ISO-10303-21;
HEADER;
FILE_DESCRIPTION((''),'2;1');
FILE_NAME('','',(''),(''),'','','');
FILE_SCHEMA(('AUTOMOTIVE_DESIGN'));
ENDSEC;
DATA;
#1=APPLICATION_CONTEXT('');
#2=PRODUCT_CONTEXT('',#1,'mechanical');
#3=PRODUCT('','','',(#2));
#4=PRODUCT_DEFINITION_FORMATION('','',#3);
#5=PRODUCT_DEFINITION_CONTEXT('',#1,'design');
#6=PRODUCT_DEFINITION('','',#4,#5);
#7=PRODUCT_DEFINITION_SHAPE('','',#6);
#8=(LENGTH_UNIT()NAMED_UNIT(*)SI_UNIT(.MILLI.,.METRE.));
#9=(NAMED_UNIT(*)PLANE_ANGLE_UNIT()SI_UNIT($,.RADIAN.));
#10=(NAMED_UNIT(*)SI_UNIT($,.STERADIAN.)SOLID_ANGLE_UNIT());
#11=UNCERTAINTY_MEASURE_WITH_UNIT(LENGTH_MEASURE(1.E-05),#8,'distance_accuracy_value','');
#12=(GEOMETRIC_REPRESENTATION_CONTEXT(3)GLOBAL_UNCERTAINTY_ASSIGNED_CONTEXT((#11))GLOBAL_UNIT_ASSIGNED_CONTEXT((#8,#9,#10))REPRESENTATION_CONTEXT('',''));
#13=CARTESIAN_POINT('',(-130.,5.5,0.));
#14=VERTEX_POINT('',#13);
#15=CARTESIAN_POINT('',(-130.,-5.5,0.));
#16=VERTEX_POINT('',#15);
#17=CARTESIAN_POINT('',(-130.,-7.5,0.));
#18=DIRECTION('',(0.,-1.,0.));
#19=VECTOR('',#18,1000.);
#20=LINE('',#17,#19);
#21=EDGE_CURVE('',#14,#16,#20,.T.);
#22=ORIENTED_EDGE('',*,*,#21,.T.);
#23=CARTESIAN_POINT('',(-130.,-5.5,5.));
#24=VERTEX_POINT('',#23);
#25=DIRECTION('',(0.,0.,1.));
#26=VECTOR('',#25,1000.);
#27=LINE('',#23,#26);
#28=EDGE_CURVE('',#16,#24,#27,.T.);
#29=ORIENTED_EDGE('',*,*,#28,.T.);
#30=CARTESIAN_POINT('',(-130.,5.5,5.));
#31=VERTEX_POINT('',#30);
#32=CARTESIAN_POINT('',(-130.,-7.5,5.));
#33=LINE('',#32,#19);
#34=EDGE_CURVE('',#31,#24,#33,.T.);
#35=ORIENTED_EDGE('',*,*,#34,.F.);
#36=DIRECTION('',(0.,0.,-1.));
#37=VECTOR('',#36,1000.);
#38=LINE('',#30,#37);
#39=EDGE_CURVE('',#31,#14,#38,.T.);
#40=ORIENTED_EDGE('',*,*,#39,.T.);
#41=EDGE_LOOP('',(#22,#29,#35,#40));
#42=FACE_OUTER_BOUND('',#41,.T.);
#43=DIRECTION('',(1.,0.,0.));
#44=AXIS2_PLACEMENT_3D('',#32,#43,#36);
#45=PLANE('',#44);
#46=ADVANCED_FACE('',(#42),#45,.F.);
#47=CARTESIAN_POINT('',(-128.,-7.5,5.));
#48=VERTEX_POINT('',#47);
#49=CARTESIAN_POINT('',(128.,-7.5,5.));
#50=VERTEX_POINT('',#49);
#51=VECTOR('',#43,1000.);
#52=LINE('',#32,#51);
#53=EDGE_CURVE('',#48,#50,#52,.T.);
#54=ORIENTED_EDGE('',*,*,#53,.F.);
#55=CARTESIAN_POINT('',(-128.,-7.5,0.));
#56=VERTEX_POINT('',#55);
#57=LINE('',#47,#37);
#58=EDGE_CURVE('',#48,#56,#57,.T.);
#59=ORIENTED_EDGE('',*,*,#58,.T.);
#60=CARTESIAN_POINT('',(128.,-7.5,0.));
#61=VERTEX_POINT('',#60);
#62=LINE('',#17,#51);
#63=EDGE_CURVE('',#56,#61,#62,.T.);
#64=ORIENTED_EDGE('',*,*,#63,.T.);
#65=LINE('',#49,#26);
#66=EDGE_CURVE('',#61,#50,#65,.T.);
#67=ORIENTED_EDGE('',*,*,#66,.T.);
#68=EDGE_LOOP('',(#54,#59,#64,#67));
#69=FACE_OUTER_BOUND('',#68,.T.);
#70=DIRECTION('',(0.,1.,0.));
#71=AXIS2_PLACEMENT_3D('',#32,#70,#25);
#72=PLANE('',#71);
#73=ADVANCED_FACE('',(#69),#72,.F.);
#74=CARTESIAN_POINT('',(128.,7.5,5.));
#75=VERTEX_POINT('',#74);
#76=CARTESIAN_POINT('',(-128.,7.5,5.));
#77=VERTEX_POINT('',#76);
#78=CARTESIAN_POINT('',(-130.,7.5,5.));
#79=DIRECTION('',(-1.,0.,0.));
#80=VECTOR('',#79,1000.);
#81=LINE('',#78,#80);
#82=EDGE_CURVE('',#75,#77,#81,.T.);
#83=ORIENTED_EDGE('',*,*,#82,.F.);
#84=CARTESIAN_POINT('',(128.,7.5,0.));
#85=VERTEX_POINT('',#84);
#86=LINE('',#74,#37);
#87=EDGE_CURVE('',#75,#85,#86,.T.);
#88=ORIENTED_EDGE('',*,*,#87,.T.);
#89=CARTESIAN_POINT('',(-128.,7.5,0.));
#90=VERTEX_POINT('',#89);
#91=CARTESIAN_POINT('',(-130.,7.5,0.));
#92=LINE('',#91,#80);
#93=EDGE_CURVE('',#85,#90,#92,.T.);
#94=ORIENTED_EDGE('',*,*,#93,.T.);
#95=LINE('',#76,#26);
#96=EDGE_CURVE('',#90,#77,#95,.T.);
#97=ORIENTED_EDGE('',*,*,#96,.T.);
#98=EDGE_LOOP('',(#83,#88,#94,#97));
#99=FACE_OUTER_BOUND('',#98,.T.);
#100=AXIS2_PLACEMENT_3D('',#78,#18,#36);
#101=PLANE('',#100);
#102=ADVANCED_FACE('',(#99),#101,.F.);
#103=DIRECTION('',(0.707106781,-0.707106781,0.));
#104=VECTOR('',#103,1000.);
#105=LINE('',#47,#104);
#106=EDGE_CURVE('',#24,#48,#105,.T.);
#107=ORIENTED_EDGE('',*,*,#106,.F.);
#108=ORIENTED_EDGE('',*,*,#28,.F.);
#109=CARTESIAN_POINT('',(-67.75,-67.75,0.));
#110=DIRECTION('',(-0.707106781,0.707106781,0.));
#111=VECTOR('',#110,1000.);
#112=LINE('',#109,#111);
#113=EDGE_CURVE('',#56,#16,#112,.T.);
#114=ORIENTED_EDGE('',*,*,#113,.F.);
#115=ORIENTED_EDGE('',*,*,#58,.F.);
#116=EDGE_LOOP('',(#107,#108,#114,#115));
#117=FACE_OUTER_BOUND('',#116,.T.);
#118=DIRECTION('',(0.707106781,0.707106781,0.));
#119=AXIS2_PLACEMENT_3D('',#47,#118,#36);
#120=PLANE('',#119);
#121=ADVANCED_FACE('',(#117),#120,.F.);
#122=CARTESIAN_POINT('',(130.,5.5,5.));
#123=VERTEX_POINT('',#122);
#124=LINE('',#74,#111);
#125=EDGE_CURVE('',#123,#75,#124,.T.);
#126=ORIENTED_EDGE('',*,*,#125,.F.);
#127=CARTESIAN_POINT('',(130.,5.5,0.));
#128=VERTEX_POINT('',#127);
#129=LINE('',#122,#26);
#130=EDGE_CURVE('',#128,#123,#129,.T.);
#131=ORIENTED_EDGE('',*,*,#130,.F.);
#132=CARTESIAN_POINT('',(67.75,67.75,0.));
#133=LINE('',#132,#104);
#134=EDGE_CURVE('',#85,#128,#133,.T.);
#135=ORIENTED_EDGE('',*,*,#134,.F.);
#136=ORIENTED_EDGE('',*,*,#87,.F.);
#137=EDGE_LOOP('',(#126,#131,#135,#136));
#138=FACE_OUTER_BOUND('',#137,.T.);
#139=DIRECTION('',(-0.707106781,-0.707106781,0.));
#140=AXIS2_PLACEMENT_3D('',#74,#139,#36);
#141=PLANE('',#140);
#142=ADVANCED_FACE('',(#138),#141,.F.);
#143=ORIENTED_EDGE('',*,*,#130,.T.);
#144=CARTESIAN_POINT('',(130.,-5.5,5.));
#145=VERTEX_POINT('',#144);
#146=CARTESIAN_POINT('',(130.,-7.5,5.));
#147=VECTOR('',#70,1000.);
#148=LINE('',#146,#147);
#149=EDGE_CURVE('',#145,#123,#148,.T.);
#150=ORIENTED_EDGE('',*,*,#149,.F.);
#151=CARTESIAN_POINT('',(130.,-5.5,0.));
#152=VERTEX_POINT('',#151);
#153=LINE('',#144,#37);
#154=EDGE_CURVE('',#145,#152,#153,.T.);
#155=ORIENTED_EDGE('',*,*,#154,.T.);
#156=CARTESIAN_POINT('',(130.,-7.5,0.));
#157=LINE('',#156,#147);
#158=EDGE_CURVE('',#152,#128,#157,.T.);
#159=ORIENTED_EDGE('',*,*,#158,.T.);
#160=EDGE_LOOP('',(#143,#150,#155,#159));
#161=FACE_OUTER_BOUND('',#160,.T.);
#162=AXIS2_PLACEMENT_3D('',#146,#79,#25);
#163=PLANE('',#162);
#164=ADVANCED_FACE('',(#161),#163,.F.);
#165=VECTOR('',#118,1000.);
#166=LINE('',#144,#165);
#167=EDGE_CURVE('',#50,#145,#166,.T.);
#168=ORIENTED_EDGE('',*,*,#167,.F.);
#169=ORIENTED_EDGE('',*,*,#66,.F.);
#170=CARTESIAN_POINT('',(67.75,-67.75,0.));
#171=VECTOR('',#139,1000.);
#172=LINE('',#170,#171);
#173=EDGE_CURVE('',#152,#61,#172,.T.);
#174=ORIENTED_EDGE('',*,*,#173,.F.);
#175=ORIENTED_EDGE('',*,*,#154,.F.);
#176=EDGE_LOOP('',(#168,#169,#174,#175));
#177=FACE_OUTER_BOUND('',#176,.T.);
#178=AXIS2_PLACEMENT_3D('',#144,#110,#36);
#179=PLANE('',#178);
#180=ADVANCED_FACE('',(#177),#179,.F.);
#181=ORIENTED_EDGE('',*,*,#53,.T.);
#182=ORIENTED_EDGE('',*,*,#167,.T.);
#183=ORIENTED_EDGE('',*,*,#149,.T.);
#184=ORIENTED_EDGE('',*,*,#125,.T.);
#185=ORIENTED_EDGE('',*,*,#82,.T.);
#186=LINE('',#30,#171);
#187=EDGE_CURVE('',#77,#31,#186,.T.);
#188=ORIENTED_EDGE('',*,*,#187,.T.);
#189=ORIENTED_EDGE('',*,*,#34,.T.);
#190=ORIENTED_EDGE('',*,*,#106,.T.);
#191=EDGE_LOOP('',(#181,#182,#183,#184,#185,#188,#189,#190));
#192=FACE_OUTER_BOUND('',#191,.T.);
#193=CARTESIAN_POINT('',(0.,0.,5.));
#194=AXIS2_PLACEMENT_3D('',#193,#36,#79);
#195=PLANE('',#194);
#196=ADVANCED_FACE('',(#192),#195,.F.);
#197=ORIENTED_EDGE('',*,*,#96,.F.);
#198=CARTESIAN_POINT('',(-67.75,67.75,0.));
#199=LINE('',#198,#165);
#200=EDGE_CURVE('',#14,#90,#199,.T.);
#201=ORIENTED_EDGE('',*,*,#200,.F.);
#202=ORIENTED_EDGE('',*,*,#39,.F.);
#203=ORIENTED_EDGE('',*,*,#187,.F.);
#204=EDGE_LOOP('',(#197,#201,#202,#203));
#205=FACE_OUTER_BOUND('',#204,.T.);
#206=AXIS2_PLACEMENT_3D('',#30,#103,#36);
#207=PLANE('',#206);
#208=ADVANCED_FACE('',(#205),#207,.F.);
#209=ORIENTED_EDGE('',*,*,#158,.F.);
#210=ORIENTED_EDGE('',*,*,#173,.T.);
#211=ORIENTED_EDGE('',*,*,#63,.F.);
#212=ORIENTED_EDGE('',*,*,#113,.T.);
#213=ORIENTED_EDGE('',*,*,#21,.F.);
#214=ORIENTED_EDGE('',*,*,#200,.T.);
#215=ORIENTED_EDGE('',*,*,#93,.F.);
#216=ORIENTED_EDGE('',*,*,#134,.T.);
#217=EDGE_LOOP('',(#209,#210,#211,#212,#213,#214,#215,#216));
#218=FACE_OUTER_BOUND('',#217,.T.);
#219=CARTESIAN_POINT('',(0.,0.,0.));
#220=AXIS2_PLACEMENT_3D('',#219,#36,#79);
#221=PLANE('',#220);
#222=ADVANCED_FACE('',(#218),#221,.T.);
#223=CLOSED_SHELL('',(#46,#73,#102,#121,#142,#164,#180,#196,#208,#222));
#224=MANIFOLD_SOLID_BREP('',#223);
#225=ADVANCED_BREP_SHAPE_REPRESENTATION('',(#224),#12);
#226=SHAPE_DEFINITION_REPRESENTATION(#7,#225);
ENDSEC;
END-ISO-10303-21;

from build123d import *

# Parameters (mm, degrees)
SKETCH_1_W      = 260
SKETCH_1_H      = 15
EXTRUDE_1_DEPTH = 5
CHAMFER_1_SIZE  = 2


with BuildPart() as part:
    # 草图1 → 凸台-拉伸1 (new body)
    with BuildSketch(Plane.XY):
        Rectangle(SKETCH_1_W, SKETCH_1_H)
    extrude(amount=EXTRUDE_1_DEPTH)

    # 倒角1
    chamfer_1_edges = [part.edges().sort_by_distance(p)[0] for p in [
        (130, -7.5, 2.5),
        (-130, -7.5, 2.5),
        (-130, 7.5, 2.5),
        (130, 7.5, 2.5),
    ]]
    chamfer(chamfer_1_edges, length=CHAMFER_1_SIZE)


solid = part.part
